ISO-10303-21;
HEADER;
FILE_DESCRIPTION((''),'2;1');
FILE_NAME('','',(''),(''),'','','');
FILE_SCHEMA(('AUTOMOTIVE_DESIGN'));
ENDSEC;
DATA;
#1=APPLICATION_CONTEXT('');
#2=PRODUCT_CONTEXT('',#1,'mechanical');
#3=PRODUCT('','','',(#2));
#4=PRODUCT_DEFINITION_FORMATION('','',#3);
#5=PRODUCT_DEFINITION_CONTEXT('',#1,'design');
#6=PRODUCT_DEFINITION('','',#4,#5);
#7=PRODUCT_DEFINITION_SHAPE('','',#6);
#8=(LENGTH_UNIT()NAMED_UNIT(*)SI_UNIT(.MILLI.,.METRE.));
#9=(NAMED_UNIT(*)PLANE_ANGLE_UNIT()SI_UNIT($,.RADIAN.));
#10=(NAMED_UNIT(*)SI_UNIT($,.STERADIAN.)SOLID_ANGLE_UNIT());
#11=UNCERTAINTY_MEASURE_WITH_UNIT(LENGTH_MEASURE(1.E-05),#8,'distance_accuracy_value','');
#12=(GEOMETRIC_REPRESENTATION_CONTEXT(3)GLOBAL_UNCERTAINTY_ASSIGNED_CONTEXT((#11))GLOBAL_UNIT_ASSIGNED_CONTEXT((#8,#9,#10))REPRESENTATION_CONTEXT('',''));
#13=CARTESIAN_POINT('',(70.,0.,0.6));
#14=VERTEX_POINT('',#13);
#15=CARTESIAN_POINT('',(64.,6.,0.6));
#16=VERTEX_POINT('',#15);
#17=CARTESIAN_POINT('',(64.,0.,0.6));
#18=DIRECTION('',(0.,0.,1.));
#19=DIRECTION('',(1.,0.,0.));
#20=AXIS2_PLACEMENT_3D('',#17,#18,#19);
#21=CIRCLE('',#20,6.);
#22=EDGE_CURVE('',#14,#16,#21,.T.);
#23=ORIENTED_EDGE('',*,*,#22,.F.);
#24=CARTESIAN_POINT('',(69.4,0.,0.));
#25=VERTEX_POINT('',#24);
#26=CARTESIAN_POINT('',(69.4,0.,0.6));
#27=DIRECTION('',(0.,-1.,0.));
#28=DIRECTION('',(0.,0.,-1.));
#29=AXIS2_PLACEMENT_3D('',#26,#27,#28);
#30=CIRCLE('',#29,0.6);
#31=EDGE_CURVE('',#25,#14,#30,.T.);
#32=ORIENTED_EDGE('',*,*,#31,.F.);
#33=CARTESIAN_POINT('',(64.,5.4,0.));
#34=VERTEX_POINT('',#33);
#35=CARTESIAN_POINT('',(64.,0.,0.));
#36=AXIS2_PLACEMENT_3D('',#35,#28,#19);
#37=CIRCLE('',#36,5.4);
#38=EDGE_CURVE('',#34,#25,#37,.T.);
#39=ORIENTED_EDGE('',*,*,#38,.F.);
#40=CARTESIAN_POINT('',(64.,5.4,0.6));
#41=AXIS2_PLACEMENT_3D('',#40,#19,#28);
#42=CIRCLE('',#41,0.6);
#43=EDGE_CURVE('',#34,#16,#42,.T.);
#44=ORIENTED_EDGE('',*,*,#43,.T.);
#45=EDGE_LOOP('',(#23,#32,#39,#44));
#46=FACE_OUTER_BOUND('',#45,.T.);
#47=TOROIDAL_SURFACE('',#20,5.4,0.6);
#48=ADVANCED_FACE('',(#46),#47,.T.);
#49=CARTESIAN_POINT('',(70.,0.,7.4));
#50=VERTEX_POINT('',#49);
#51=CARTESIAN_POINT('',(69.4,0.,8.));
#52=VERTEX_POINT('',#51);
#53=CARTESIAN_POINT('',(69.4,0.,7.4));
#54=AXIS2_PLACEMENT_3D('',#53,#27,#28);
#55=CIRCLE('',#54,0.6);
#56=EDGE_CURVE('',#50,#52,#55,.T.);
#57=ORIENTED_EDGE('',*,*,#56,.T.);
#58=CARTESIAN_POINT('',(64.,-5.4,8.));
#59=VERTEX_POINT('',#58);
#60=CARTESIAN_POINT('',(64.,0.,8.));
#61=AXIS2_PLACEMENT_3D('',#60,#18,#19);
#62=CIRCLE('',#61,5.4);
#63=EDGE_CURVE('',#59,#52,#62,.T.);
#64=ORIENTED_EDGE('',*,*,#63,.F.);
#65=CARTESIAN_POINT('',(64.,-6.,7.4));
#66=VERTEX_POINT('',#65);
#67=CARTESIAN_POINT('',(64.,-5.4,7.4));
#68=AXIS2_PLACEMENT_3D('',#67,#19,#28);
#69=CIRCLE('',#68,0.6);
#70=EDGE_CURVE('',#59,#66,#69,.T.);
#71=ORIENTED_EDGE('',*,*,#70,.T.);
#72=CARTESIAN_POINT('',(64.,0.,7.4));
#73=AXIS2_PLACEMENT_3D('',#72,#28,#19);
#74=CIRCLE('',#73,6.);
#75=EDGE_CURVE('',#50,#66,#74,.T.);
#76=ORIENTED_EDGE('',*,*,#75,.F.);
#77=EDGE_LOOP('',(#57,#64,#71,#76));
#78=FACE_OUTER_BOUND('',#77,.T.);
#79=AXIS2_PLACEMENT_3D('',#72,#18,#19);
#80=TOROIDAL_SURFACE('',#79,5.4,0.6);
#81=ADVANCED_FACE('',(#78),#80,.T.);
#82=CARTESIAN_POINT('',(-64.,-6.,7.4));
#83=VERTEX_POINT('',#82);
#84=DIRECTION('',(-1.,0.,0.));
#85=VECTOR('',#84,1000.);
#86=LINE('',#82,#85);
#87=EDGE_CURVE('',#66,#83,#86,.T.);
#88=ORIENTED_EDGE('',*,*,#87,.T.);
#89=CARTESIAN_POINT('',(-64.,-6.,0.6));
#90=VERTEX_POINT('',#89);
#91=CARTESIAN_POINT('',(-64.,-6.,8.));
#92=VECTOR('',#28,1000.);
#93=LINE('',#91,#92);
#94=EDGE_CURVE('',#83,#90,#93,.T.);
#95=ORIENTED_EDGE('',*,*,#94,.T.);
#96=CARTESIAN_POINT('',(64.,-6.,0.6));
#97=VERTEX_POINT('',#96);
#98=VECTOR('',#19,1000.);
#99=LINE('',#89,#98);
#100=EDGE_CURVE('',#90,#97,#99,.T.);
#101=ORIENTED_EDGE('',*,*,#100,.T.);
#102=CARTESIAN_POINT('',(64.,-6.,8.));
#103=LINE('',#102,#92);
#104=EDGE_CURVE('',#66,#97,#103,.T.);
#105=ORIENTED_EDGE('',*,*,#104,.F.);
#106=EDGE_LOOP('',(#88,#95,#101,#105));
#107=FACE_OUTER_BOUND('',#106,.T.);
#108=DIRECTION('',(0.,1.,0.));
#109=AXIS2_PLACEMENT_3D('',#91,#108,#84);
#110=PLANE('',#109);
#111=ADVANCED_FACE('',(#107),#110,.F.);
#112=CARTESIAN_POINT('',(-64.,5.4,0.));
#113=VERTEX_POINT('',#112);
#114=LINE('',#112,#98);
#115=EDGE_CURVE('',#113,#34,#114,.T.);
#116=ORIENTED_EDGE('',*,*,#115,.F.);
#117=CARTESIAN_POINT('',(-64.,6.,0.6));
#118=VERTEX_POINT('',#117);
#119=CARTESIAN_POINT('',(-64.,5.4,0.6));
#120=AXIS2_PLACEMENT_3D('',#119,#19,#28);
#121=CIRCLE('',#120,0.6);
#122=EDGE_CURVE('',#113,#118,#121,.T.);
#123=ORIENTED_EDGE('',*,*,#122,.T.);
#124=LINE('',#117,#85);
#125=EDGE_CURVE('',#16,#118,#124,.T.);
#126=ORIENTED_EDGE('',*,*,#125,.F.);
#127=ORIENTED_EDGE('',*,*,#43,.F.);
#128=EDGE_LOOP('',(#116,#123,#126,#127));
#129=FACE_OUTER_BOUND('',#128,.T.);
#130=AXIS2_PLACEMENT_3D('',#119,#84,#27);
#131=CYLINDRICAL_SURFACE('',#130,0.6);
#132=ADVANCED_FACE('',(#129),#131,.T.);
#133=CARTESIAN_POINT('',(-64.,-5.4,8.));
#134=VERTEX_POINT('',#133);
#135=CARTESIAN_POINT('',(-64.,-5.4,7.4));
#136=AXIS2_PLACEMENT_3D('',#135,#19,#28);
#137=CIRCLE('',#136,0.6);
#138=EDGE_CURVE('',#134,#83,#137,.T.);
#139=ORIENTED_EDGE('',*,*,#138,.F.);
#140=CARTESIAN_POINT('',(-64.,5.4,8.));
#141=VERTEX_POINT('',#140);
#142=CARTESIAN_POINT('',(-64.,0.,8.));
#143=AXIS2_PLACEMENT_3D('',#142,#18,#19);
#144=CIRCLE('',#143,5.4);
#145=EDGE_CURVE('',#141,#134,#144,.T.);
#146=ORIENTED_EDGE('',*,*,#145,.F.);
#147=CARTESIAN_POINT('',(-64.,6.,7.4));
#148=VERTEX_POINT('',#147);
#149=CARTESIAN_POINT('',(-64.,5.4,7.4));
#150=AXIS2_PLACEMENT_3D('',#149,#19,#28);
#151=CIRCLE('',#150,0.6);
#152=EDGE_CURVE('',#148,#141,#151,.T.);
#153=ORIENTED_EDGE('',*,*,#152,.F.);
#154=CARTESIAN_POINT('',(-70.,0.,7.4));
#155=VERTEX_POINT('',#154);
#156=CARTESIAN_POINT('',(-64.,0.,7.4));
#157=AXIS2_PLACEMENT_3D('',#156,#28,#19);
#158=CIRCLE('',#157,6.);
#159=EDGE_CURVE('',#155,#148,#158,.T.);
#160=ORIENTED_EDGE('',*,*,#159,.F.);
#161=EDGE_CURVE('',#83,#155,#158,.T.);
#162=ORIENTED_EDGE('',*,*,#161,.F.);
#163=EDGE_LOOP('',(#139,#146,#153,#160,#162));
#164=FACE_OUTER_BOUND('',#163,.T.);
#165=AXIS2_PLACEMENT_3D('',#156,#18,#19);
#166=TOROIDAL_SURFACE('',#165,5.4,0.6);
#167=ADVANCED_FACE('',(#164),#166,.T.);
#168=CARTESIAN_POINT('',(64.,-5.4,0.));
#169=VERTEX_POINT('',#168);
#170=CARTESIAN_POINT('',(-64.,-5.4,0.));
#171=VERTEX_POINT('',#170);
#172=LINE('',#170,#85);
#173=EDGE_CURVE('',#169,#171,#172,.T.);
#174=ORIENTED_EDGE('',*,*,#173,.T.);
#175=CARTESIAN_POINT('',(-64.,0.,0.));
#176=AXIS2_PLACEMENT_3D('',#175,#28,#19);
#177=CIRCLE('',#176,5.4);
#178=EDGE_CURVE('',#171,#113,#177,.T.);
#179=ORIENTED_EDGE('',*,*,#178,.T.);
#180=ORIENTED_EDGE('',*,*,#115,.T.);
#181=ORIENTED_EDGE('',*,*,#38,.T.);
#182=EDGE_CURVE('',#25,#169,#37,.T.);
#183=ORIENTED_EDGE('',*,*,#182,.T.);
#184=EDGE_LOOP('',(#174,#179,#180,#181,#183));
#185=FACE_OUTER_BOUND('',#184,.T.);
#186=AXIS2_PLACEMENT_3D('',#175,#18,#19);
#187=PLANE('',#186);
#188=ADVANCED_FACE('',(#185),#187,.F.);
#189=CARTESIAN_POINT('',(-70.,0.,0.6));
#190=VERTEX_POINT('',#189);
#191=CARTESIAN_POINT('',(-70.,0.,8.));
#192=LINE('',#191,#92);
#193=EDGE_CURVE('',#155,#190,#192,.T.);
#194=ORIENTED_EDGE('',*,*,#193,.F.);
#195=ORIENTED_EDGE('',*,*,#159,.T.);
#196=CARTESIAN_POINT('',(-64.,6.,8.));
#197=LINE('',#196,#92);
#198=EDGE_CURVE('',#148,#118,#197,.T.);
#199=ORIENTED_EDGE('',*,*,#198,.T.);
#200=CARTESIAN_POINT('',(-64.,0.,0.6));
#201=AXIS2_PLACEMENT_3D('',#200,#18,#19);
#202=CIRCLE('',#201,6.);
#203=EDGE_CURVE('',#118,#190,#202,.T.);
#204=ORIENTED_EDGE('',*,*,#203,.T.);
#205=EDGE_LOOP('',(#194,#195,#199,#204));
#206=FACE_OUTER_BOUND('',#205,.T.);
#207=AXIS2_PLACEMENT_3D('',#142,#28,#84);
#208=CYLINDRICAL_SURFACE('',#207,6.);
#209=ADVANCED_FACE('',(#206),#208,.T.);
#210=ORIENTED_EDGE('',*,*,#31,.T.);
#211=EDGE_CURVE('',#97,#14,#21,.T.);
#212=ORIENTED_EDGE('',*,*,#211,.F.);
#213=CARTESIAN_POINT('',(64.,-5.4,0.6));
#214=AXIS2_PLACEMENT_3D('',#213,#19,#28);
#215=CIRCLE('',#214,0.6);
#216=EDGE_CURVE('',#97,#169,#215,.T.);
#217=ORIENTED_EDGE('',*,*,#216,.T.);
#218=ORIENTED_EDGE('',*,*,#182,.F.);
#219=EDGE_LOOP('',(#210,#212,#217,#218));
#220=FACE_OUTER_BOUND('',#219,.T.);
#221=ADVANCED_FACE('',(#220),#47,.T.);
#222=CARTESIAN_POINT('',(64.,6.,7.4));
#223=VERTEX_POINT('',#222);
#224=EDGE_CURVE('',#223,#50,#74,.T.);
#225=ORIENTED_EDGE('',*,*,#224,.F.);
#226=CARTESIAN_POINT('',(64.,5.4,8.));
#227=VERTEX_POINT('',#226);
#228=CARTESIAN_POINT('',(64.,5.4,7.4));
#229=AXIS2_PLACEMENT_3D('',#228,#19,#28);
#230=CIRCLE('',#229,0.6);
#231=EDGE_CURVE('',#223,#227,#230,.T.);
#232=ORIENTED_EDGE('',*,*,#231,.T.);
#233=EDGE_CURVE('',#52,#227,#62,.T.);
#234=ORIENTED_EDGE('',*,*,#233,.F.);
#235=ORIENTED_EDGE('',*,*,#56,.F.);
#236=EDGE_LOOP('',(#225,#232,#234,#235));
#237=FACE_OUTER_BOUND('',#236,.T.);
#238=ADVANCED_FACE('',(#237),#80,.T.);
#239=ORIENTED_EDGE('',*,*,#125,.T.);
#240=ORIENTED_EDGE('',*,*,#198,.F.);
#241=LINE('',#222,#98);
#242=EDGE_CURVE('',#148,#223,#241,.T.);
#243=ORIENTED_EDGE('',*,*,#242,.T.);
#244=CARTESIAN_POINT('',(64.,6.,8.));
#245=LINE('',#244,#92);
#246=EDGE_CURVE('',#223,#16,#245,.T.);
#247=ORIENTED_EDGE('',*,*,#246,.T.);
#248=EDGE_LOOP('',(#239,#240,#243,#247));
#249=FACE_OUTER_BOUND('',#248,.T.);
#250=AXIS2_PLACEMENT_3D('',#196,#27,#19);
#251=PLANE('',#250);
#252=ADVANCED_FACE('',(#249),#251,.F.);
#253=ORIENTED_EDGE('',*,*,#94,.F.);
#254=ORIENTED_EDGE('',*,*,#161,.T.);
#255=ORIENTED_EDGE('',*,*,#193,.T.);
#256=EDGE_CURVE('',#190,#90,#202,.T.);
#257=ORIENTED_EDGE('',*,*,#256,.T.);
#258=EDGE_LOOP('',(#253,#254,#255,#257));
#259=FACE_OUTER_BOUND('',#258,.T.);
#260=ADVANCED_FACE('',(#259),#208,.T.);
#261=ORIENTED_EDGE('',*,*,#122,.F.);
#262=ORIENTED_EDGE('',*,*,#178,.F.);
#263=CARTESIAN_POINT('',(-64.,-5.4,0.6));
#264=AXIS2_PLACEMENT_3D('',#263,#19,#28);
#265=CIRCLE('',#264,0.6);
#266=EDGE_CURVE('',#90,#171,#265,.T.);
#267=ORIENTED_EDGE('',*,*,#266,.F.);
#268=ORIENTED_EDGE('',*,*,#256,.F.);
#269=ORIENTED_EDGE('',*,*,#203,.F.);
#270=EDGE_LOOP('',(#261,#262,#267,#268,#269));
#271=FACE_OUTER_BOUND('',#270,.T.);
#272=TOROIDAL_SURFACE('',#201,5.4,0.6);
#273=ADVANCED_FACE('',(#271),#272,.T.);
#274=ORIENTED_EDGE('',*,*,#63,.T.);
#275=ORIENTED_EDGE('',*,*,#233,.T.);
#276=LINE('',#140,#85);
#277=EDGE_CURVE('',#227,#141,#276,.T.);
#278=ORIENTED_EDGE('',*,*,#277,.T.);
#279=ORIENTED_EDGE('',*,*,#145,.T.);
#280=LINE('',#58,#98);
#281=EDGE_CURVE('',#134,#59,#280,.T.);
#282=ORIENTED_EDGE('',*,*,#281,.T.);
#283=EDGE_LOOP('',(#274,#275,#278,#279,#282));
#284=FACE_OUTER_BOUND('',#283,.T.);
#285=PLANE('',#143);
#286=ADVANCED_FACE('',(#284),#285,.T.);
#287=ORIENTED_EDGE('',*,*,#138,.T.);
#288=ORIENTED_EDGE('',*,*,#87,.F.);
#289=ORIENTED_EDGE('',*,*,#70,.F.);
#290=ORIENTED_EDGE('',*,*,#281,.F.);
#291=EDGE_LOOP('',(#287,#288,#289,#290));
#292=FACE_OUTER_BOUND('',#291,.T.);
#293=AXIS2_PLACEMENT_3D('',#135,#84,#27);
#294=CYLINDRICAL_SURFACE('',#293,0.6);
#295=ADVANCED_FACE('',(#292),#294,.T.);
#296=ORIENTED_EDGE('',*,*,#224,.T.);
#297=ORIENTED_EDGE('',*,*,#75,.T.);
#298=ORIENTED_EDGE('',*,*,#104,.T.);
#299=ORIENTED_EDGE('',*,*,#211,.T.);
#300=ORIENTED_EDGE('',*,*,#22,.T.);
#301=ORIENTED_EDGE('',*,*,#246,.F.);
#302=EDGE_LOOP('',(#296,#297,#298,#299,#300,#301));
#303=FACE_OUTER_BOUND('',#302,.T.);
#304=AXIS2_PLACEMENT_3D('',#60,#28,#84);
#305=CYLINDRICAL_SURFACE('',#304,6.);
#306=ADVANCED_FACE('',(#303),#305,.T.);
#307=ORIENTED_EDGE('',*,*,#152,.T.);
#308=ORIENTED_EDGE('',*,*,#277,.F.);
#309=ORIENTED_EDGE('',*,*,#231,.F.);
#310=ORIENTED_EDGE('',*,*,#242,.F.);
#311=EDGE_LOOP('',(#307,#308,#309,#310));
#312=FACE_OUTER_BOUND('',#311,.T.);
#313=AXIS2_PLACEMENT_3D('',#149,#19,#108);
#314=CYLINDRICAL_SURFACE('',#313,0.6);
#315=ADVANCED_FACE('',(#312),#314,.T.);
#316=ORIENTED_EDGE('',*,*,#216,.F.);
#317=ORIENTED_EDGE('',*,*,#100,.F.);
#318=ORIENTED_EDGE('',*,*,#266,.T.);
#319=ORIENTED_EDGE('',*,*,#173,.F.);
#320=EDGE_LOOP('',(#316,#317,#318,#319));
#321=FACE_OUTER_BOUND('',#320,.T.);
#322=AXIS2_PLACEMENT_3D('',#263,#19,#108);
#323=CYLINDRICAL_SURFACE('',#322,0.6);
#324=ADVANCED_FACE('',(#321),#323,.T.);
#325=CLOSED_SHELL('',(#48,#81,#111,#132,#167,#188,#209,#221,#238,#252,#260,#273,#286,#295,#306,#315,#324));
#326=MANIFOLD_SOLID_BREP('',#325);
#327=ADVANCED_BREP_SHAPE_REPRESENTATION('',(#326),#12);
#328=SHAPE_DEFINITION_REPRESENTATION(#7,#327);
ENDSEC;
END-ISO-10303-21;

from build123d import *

# Parameters (mm, degrees)
EXTRUDE_523_DEPTH = 8
FILLET_1_R        = 0.6


with BuildPart() as part:
    # 草图1 → Extrude 523 (new body)
    with BuildSketch(Plane.XY):
        with BuildLine():
            Line((-64, 6), (64, 6))
            ThreePointArc((64, 6), (70, 0), (64, -6))
            Line((64, -6), (-64, -6))
            ThreePointArc((-64, -6), (-70, 0), (-64, 6))
        make_face()
    extrude(amount=EXTRUDE_523_DEPTH)

    # 圆角1
    fillet_1_edges = [part.edges().sort_by_distance(p)[0] for p in [
        (70, 0, 8),
        (0, 6, 8),
        (-70, 0, 8),
        (0, 6, 0),
        (70, 0, 0),
        (0, -6, 0),
        (-70, 0, 0),
        (0, -6, 8),
    ]]
    fillet(fillet_1_edges, radius=FILLET_1_R)


solid = part.part
